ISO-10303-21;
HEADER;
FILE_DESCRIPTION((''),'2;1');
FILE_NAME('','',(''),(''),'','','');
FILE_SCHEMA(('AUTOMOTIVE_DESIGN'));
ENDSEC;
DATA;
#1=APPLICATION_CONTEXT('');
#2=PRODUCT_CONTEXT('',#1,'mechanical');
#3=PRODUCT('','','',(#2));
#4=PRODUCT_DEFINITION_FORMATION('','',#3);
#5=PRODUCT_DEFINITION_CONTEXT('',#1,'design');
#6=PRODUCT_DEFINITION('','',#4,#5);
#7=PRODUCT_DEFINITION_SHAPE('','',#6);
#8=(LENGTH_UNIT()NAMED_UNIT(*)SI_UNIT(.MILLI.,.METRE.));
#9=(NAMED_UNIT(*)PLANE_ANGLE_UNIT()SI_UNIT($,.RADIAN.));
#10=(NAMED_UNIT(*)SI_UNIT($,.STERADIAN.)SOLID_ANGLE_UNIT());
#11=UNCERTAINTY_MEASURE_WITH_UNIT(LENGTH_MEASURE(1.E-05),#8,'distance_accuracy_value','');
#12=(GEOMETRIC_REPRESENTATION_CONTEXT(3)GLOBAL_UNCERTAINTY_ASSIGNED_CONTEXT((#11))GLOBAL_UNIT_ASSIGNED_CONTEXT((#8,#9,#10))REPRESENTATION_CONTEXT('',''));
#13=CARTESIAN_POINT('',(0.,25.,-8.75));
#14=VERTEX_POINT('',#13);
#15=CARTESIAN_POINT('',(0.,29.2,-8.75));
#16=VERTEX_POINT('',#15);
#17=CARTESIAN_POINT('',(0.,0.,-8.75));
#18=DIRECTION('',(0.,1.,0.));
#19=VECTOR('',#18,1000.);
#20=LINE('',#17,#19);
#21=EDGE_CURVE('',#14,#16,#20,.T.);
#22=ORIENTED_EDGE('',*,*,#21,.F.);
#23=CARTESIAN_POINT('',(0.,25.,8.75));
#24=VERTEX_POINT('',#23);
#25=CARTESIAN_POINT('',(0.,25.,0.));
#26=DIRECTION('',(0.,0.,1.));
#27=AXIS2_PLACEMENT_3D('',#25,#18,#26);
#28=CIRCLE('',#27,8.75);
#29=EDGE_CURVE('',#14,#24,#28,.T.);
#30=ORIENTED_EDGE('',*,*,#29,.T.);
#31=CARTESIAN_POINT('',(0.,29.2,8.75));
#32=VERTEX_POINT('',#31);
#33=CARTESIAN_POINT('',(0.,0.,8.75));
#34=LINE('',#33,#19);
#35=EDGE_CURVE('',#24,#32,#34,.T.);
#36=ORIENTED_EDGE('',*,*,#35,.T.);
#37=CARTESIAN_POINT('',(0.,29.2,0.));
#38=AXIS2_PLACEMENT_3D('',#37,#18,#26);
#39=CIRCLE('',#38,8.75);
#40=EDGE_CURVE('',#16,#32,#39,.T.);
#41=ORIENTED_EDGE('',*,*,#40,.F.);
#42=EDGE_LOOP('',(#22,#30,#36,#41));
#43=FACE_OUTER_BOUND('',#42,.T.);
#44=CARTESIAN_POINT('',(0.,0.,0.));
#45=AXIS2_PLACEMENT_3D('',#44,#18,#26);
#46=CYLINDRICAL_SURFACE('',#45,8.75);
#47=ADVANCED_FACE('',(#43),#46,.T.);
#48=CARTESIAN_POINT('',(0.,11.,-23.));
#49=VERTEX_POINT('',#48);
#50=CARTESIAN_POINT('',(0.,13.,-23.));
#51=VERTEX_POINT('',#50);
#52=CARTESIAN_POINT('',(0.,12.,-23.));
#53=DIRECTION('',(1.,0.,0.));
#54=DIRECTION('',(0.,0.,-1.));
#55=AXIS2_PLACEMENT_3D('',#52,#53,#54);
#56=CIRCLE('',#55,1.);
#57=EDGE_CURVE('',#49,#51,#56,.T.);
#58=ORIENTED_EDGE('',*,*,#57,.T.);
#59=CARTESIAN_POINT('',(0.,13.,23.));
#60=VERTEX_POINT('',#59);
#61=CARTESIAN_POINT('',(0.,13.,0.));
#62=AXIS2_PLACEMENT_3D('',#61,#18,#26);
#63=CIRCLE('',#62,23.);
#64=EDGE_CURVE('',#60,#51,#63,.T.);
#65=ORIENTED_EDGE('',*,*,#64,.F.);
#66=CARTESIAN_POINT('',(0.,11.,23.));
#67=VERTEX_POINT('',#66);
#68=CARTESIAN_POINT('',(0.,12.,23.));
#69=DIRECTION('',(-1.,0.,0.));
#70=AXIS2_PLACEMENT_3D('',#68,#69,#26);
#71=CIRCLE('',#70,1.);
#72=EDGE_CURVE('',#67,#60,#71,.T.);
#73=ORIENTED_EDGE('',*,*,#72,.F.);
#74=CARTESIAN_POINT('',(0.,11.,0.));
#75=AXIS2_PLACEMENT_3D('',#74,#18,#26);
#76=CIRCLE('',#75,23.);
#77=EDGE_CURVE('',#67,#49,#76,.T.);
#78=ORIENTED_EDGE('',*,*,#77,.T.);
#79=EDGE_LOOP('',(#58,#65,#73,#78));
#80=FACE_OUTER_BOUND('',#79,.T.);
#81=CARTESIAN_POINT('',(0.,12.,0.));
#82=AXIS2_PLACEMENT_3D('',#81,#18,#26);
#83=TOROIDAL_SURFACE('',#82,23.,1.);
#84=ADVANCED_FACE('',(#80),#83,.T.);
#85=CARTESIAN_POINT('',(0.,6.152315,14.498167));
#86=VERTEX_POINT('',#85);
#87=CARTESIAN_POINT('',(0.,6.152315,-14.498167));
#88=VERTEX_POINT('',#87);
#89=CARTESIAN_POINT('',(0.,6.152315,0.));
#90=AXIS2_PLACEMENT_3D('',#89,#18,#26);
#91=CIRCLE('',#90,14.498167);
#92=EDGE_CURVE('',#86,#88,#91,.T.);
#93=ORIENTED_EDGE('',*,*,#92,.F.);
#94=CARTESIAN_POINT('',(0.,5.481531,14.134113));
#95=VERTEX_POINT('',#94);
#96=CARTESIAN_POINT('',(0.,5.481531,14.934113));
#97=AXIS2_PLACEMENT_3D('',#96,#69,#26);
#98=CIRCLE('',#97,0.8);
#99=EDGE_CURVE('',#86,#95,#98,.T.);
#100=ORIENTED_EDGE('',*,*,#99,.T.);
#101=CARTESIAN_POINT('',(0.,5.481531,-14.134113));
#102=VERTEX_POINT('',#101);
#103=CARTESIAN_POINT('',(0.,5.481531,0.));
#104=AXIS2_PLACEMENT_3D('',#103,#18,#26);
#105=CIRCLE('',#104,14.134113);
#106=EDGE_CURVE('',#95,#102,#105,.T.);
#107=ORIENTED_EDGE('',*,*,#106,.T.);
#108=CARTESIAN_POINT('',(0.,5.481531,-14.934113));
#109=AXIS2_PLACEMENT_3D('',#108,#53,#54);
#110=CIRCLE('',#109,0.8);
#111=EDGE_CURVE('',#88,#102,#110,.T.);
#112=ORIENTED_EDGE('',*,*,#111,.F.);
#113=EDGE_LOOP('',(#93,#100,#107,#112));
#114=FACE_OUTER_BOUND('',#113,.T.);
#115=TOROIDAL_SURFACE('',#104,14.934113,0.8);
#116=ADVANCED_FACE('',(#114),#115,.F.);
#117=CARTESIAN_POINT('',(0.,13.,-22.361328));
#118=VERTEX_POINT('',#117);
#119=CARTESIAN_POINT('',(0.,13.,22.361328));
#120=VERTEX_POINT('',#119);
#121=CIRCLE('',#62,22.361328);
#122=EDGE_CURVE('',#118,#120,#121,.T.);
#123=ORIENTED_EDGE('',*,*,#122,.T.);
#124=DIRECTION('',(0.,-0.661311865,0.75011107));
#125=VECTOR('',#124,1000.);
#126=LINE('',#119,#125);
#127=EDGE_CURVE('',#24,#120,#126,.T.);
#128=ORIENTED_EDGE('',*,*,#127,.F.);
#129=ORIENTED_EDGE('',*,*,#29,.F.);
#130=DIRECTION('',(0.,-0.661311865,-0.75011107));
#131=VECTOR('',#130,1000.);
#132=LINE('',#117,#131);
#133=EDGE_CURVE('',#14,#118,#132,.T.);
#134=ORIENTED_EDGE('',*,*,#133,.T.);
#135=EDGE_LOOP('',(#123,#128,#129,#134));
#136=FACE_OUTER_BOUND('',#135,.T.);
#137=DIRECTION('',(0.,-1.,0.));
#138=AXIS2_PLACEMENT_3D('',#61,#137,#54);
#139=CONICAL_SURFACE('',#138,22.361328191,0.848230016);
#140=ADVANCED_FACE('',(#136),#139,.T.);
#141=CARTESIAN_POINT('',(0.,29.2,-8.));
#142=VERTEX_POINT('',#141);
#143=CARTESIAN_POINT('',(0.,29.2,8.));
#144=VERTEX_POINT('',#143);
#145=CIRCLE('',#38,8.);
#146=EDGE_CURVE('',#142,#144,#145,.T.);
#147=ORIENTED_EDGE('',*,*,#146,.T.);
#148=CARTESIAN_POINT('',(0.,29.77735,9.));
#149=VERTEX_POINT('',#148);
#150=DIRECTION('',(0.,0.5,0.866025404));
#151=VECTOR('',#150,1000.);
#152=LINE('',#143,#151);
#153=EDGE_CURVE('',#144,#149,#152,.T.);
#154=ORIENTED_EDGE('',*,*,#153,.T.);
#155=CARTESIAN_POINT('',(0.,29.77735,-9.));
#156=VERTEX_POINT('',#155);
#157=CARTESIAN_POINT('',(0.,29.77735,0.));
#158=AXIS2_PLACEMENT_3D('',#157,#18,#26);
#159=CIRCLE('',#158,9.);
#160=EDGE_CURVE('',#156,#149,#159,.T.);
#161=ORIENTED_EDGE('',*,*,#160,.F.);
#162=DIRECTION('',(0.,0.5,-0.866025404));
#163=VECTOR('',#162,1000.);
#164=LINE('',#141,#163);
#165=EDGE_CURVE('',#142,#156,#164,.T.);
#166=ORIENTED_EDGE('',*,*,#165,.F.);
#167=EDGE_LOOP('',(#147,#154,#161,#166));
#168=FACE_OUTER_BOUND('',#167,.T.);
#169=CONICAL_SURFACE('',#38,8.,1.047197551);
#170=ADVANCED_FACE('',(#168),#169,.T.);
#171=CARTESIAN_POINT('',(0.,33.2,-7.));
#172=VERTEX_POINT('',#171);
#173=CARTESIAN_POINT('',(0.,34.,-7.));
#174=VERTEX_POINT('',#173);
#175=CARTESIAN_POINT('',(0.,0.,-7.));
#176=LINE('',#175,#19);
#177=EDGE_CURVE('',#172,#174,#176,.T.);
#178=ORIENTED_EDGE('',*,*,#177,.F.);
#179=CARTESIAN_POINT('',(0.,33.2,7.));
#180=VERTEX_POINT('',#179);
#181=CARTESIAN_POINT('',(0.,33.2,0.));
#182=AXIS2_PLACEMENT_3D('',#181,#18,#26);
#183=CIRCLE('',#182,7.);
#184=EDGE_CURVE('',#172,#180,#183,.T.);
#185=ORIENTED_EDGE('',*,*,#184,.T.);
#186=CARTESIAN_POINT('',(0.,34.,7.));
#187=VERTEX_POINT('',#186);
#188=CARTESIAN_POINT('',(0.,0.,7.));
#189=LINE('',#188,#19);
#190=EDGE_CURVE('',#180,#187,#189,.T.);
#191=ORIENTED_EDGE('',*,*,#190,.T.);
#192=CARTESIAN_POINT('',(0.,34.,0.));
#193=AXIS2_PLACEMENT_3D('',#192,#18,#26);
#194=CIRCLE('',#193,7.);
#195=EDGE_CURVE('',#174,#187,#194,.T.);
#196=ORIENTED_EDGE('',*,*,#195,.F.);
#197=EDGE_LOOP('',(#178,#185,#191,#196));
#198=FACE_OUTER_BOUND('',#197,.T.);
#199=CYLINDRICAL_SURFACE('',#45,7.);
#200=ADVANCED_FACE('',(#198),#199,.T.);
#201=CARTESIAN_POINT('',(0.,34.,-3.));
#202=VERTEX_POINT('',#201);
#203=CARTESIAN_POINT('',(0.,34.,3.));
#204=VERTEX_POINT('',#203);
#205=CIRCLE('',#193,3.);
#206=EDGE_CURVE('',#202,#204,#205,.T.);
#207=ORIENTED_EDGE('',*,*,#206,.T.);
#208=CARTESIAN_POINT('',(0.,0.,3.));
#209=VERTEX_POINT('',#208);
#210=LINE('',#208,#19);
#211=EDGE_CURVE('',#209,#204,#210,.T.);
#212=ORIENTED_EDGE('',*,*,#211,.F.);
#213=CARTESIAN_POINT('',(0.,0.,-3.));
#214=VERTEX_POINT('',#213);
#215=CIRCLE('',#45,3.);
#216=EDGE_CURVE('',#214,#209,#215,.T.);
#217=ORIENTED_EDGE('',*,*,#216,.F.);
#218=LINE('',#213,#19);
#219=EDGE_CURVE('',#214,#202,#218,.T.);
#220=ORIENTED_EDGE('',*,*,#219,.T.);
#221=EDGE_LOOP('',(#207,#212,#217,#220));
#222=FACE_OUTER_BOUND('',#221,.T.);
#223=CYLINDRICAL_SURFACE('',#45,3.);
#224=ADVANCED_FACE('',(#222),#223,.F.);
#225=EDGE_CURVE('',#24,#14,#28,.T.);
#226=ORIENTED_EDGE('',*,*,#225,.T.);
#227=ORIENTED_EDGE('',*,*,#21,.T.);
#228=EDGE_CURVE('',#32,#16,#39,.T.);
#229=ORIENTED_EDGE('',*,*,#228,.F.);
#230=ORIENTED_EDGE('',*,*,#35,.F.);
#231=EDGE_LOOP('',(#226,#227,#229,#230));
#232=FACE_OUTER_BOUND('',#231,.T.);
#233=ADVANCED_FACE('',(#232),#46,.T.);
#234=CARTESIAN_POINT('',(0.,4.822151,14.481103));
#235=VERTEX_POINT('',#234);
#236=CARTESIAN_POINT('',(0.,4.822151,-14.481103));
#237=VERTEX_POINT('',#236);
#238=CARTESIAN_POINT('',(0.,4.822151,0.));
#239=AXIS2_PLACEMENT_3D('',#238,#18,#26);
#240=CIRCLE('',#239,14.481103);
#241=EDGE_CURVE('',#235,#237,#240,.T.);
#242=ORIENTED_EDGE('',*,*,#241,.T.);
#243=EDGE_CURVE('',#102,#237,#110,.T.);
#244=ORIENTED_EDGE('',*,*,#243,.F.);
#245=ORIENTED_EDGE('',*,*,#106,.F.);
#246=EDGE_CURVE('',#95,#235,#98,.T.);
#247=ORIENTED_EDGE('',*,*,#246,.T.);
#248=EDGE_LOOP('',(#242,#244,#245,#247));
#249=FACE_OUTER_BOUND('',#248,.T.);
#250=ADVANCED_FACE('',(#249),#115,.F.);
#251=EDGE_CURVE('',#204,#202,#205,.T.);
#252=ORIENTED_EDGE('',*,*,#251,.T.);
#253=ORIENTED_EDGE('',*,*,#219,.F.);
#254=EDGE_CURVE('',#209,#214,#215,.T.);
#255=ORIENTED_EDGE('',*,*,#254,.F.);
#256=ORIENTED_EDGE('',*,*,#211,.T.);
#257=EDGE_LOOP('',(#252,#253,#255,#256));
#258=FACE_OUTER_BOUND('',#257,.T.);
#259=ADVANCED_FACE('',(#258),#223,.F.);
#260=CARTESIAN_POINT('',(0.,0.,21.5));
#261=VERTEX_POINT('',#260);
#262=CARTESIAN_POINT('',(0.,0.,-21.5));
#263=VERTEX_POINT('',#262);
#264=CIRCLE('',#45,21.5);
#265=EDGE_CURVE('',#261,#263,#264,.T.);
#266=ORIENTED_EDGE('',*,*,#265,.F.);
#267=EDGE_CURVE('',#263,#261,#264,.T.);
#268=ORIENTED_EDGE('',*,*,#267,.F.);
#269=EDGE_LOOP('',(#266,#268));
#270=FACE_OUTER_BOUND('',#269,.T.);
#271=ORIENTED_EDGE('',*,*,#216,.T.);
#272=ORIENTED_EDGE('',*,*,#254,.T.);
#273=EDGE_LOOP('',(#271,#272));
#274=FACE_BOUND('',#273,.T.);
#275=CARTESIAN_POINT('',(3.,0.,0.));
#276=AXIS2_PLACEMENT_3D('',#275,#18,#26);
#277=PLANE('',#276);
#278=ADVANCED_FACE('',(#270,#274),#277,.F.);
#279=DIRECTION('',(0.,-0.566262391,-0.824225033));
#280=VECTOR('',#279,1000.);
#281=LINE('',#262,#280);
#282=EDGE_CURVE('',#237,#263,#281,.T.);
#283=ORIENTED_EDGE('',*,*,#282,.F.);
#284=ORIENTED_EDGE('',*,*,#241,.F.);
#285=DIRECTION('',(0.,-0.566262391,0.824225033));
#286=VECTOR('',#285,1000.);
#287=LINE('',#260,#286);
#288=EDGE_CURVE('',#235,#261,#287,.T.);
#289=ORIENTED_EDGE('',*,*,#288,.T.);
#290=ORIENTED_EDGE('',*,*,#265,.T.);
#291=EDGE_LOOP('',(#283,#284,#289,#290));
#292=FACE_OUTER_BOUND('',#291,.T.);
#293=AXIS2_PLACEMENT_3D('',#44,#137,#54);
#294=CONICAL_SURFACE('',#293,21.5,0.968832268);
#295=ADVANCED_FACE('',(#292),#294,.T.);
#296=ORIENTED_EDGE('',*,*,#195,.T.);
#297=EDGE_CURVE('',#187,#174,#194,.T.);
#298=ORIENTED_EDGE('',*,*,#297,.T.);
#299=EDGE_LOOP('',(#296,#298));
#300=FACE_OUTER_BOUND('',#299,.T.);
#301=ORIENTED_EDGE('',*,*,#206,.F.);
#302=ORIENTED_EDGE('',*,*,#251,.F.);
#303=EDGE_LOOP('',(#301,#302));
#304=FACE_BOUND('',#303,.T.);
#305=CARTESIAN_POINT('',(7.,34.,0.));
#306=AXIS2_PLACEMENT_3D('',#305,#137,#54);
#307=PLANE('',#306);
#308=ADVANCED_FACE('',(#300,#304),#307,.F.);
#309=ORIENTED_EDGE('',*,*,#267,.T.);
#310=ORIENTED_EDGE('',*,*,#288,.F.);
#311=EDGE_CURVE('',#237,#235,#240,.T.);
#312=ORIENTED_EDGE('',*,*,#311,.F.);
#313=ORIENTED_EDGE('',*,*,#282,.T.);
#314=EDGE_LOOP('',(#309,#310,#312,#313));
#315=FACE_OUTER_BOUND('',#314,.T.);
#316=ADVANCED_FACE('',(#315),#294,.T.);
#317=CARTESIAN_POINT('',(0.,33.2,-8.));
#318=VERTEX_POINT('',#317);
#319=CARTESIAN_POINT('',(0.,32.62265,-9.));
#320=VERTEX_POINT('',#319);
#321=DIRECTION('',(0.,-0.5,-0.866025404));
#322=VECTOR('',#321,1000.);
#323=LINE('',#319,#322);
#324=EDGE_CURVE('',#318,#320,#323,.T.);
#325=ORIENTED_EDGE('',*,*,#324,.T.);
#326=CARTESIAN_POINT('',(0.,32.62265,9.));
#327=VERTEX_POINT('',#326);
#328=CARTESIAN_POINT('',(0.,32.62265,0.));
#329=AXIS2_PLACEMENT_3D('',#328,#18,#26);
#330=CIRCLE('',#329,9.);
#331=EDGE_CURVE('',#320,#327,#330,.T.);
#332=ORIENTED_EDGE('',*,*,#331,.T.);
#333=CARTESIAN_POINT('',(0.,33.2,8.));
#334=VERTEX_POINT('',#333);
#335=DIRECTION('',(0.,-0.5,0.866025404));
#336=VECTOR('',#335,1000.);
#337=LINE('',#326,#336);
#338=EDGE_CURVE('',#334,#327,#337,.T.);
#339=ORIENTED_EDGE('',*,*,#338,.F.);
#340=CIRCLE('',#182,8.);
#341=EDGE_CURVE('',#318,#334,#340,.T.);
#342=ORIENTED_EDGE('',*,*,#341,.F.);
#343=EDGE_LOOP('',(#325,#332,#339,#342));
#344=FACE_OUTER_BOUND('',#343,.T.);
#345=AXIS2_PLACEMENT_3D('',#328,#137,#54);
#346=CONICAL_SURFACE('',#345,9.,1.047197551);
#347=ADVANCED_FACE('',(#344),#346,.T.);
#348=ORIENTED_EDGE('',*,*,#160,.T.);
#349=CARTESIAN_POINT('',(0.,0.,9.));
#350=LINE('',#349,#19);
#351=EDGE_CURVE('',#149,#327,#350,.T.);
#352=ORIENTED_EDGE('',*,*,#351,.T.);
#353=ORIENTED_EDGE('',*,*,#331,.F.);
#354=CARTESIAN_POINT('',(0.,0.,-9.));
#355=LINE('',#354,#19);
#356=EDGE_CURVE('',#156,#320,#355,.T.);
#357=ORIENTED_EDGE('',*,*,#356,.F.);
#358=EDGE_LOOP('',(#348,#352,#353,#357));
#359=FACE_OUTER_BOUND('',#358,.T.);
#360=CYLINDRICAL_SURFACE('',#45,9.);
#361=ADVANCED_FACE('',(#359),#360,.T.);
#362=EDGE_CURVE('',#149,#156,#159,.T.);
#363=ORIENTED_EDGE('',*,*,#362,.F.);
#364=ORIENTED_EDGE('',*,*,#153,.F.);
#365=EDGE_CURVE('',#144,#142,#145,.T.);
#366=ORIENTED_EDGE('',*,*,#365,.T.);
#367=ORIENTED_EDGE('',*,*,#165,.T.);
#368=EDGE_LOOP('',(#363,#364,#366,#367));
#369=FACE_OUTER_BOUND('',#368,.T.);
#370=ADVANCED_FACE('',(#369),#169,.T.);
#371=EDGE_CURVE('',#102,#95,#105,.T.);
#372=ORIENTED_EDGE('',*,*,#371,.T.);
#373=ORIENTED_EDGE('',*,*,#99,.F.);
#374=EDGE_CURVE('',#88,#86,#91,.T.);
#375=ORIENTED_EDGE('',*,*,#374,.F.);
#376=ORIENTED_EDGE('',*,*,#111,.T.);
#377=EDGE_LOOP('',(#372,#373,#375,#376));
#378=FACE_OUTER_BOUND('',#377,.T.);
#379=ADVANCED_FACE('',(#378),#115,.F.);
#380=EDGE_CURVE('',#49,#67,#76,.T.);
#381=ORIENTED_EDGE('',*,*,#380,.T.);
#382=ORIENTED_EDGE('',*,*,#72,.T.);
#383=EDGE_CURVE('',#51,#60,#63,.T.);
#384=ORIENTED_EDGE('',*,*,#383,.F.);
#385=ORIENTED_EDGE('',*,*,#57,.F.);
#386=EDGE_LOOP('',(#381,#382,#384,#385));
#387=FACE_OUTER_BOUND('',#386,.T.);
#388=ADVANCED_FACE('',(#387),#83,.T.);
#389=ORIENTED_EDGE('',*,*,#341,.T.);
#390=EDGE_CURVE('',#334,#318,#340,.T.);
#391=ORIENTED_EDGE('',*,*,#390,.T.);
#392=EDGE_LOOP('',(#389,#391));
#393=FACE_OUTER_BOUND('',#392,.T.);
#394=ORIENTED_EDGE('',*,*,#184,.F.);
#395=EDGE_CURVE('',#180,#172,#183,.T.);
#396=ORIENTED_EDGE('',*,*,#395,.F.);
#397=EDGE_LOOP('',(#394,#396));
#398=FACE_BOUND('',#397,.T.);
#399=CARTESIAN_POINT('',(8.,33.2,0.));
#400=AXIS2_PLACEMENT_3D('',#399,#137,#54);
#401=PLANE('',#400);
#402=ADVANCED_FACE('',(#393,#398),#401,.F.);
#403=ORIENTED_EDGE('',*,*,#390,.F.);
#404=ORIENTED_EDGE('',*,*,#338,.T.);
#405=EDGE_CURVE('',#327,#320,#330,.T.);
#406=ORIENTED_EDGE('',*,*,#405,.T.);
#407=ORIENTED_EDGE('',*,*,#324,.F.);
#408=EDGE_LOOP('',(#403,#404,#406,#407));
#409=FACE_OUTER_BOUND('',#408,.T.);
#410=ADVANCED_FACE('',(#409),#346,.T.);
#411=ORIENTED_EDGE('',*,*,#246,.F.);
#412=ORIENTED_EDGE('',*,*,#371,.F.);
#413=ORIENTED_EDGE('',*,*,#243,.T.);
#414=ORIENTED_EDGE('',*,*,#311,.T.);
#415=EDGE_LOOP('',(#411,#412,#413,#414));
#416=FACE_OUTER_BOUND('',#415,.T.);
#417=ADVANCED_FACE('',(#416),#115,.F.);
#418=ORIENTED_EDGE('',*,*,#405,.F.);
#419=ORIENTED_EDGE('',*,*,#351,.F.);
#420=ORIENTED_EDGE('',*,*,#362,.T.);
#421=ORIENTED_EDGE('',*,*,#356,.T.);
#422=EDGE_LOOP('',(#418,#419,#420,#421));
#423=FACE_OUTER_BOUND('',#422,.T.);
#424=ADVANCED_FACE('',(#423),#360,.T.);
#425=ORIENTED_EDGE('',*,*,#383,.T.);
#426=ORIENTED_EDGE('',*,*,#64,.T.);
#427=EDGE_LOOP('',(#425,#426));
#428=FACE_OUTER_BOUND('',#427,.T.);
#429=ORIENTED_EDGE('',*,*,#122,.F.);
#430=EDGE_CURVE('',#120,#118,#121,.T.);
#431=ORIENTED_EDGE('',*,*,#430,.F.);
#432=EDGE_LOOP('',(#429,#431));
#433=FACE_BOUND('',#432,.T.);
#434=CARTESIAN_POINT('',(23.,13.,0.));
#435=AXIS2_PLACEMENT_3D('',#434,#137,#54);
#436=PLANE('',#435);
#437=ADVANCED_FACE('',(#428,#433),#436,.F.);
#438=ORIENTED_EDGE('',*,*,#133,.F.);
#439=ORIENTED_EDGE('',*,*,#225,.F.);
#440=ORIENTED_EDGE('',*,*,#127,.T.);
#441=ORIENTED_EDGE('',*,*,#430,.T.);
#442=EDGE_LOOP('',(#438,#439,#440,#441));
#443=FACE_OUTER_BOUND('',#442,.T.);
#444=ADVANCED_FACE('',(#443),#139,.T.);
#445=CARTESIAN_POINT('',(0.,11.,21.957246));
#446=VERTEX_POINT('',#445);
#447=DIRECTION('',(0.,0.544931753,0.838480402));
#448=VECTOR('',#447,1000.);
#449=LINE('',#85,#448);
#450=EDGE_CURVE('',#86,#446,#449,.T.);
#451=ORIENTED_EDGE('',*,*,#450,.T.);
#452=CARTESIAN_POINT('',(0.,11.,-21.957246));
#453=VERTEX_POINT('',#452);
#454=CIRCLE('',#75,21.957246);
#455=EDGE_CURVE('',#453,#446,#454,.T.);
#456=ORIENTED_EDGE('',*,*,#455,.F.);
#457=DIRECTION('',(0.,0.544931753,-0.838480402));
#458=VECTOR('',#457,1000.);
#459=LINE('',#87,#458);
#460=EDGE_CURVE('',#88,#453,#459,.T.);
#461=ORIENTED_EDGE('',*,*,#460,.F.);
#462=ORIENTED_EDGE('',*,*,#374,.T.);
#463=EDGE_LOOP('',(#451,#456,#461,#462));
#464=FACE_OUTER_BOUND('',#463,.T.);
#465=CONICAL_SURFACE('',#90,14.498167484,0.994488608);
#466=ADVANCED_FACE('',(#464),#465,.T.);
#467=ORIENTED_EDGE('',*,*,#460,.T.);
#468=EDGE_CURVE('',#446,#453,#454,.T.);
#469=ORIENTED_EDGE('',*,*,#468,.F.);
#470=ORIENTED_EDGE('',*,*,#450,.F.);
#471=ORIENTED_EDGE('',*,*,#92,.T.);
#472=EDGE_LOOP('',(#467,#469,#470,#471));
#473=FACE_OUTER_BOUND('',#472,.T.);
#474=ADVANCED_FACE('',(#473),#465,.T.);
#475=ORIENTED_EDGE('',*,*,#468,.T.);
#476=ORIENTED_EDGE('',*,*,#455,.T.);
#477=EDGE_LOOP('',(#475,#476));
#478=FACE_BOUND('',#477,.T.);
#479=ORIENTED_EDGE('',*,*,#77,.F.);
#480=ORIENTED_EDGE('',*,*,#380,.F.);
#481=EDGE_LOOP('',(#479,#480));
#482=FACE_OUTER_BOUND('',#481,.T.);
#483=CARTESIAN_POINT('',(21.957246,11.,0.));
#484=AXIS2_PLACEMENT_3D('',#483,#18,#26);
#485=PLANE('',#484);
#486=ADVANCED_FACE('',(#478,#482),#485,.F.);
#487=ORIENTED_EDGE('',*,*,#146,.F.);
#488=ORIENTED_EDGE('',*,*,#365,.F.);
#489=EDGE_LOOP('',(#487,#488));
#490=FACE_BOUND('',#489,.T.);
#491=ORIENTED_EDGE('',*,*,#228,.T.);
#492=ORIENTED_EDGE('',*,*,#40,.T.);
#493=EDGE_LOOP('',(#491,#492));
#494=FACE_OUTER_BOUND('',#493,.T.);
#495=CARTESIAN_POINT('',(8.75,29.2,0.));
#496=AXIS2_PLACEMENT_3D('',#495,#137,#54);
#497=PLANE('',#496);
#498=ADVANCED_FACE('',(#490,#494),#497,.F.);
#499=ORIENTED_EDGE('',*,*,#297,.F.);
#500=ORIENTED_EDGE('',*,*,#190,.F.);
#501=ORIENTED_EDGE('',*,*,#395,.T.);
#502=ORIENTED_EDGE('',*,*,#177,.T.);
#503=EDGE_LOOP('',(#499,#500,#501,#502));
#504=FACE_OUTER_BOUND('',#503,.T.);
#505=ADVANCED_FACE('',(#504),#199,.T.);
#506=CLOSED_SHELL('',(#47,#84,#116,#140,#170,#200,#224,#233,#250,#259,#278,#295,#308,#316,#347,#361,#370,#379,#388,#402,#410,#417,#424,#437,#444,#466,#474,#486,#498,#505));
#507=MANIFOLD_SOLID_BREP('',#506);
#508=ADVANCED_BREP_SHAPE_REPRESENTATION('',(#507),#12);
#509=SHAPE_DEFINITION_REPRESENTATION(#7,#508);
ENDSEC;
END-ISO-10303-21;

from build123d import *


with BuildPart() as part:
    # Sketch1 → Revolve1 (revolve)
    with BuildSketch(Plane.XY, mode=Mode.PRIVATE) as revolve1_sk:
        with BuildLine():
            Line((3, 0), (21.5, 0))
            Line((21.5, 0), (14.481102974, 4.822150816))
            ThreePointArc((14.481102974, 4.822150816), (14.13417871, 5.491793096), (14.498167484, 6.152315163))
            Line((14.498167484, 6.152315163), (21.957245997, 11))
            Line((21.957245997, 11), (23, 11))
            ThreePointArc((23, 11), (24, 12), (23, 13))
            Line((23, 13), (22.361328191, 13))
            Line((22.361328191, 13), (8.75, 25))
            Line((8.75, 25), (8.75, 29.2))
            Line((8.75, 29.2), (8, 29.2))
            Line((8, 29.2), (9, 29.777350269))
            Line((9, 29.777350269), (9, 32.622649731))
            Line((9, 32.622649731), (8, 33.2))
            Line((8, 33.2), (7, 33.2))
            Line((7, 33.2), (7, 34))
            Line((7, 34), (3, 34))
            Line((3, 34), (3, 0))
        make_face()
    revolve(revolve1_sk.sketch.rotate(Axis((0, 0, 0), (0, 1, 0)), 270), axis=Axis((0, 0, 0), (0, 1, 0)))


solid = part.part
